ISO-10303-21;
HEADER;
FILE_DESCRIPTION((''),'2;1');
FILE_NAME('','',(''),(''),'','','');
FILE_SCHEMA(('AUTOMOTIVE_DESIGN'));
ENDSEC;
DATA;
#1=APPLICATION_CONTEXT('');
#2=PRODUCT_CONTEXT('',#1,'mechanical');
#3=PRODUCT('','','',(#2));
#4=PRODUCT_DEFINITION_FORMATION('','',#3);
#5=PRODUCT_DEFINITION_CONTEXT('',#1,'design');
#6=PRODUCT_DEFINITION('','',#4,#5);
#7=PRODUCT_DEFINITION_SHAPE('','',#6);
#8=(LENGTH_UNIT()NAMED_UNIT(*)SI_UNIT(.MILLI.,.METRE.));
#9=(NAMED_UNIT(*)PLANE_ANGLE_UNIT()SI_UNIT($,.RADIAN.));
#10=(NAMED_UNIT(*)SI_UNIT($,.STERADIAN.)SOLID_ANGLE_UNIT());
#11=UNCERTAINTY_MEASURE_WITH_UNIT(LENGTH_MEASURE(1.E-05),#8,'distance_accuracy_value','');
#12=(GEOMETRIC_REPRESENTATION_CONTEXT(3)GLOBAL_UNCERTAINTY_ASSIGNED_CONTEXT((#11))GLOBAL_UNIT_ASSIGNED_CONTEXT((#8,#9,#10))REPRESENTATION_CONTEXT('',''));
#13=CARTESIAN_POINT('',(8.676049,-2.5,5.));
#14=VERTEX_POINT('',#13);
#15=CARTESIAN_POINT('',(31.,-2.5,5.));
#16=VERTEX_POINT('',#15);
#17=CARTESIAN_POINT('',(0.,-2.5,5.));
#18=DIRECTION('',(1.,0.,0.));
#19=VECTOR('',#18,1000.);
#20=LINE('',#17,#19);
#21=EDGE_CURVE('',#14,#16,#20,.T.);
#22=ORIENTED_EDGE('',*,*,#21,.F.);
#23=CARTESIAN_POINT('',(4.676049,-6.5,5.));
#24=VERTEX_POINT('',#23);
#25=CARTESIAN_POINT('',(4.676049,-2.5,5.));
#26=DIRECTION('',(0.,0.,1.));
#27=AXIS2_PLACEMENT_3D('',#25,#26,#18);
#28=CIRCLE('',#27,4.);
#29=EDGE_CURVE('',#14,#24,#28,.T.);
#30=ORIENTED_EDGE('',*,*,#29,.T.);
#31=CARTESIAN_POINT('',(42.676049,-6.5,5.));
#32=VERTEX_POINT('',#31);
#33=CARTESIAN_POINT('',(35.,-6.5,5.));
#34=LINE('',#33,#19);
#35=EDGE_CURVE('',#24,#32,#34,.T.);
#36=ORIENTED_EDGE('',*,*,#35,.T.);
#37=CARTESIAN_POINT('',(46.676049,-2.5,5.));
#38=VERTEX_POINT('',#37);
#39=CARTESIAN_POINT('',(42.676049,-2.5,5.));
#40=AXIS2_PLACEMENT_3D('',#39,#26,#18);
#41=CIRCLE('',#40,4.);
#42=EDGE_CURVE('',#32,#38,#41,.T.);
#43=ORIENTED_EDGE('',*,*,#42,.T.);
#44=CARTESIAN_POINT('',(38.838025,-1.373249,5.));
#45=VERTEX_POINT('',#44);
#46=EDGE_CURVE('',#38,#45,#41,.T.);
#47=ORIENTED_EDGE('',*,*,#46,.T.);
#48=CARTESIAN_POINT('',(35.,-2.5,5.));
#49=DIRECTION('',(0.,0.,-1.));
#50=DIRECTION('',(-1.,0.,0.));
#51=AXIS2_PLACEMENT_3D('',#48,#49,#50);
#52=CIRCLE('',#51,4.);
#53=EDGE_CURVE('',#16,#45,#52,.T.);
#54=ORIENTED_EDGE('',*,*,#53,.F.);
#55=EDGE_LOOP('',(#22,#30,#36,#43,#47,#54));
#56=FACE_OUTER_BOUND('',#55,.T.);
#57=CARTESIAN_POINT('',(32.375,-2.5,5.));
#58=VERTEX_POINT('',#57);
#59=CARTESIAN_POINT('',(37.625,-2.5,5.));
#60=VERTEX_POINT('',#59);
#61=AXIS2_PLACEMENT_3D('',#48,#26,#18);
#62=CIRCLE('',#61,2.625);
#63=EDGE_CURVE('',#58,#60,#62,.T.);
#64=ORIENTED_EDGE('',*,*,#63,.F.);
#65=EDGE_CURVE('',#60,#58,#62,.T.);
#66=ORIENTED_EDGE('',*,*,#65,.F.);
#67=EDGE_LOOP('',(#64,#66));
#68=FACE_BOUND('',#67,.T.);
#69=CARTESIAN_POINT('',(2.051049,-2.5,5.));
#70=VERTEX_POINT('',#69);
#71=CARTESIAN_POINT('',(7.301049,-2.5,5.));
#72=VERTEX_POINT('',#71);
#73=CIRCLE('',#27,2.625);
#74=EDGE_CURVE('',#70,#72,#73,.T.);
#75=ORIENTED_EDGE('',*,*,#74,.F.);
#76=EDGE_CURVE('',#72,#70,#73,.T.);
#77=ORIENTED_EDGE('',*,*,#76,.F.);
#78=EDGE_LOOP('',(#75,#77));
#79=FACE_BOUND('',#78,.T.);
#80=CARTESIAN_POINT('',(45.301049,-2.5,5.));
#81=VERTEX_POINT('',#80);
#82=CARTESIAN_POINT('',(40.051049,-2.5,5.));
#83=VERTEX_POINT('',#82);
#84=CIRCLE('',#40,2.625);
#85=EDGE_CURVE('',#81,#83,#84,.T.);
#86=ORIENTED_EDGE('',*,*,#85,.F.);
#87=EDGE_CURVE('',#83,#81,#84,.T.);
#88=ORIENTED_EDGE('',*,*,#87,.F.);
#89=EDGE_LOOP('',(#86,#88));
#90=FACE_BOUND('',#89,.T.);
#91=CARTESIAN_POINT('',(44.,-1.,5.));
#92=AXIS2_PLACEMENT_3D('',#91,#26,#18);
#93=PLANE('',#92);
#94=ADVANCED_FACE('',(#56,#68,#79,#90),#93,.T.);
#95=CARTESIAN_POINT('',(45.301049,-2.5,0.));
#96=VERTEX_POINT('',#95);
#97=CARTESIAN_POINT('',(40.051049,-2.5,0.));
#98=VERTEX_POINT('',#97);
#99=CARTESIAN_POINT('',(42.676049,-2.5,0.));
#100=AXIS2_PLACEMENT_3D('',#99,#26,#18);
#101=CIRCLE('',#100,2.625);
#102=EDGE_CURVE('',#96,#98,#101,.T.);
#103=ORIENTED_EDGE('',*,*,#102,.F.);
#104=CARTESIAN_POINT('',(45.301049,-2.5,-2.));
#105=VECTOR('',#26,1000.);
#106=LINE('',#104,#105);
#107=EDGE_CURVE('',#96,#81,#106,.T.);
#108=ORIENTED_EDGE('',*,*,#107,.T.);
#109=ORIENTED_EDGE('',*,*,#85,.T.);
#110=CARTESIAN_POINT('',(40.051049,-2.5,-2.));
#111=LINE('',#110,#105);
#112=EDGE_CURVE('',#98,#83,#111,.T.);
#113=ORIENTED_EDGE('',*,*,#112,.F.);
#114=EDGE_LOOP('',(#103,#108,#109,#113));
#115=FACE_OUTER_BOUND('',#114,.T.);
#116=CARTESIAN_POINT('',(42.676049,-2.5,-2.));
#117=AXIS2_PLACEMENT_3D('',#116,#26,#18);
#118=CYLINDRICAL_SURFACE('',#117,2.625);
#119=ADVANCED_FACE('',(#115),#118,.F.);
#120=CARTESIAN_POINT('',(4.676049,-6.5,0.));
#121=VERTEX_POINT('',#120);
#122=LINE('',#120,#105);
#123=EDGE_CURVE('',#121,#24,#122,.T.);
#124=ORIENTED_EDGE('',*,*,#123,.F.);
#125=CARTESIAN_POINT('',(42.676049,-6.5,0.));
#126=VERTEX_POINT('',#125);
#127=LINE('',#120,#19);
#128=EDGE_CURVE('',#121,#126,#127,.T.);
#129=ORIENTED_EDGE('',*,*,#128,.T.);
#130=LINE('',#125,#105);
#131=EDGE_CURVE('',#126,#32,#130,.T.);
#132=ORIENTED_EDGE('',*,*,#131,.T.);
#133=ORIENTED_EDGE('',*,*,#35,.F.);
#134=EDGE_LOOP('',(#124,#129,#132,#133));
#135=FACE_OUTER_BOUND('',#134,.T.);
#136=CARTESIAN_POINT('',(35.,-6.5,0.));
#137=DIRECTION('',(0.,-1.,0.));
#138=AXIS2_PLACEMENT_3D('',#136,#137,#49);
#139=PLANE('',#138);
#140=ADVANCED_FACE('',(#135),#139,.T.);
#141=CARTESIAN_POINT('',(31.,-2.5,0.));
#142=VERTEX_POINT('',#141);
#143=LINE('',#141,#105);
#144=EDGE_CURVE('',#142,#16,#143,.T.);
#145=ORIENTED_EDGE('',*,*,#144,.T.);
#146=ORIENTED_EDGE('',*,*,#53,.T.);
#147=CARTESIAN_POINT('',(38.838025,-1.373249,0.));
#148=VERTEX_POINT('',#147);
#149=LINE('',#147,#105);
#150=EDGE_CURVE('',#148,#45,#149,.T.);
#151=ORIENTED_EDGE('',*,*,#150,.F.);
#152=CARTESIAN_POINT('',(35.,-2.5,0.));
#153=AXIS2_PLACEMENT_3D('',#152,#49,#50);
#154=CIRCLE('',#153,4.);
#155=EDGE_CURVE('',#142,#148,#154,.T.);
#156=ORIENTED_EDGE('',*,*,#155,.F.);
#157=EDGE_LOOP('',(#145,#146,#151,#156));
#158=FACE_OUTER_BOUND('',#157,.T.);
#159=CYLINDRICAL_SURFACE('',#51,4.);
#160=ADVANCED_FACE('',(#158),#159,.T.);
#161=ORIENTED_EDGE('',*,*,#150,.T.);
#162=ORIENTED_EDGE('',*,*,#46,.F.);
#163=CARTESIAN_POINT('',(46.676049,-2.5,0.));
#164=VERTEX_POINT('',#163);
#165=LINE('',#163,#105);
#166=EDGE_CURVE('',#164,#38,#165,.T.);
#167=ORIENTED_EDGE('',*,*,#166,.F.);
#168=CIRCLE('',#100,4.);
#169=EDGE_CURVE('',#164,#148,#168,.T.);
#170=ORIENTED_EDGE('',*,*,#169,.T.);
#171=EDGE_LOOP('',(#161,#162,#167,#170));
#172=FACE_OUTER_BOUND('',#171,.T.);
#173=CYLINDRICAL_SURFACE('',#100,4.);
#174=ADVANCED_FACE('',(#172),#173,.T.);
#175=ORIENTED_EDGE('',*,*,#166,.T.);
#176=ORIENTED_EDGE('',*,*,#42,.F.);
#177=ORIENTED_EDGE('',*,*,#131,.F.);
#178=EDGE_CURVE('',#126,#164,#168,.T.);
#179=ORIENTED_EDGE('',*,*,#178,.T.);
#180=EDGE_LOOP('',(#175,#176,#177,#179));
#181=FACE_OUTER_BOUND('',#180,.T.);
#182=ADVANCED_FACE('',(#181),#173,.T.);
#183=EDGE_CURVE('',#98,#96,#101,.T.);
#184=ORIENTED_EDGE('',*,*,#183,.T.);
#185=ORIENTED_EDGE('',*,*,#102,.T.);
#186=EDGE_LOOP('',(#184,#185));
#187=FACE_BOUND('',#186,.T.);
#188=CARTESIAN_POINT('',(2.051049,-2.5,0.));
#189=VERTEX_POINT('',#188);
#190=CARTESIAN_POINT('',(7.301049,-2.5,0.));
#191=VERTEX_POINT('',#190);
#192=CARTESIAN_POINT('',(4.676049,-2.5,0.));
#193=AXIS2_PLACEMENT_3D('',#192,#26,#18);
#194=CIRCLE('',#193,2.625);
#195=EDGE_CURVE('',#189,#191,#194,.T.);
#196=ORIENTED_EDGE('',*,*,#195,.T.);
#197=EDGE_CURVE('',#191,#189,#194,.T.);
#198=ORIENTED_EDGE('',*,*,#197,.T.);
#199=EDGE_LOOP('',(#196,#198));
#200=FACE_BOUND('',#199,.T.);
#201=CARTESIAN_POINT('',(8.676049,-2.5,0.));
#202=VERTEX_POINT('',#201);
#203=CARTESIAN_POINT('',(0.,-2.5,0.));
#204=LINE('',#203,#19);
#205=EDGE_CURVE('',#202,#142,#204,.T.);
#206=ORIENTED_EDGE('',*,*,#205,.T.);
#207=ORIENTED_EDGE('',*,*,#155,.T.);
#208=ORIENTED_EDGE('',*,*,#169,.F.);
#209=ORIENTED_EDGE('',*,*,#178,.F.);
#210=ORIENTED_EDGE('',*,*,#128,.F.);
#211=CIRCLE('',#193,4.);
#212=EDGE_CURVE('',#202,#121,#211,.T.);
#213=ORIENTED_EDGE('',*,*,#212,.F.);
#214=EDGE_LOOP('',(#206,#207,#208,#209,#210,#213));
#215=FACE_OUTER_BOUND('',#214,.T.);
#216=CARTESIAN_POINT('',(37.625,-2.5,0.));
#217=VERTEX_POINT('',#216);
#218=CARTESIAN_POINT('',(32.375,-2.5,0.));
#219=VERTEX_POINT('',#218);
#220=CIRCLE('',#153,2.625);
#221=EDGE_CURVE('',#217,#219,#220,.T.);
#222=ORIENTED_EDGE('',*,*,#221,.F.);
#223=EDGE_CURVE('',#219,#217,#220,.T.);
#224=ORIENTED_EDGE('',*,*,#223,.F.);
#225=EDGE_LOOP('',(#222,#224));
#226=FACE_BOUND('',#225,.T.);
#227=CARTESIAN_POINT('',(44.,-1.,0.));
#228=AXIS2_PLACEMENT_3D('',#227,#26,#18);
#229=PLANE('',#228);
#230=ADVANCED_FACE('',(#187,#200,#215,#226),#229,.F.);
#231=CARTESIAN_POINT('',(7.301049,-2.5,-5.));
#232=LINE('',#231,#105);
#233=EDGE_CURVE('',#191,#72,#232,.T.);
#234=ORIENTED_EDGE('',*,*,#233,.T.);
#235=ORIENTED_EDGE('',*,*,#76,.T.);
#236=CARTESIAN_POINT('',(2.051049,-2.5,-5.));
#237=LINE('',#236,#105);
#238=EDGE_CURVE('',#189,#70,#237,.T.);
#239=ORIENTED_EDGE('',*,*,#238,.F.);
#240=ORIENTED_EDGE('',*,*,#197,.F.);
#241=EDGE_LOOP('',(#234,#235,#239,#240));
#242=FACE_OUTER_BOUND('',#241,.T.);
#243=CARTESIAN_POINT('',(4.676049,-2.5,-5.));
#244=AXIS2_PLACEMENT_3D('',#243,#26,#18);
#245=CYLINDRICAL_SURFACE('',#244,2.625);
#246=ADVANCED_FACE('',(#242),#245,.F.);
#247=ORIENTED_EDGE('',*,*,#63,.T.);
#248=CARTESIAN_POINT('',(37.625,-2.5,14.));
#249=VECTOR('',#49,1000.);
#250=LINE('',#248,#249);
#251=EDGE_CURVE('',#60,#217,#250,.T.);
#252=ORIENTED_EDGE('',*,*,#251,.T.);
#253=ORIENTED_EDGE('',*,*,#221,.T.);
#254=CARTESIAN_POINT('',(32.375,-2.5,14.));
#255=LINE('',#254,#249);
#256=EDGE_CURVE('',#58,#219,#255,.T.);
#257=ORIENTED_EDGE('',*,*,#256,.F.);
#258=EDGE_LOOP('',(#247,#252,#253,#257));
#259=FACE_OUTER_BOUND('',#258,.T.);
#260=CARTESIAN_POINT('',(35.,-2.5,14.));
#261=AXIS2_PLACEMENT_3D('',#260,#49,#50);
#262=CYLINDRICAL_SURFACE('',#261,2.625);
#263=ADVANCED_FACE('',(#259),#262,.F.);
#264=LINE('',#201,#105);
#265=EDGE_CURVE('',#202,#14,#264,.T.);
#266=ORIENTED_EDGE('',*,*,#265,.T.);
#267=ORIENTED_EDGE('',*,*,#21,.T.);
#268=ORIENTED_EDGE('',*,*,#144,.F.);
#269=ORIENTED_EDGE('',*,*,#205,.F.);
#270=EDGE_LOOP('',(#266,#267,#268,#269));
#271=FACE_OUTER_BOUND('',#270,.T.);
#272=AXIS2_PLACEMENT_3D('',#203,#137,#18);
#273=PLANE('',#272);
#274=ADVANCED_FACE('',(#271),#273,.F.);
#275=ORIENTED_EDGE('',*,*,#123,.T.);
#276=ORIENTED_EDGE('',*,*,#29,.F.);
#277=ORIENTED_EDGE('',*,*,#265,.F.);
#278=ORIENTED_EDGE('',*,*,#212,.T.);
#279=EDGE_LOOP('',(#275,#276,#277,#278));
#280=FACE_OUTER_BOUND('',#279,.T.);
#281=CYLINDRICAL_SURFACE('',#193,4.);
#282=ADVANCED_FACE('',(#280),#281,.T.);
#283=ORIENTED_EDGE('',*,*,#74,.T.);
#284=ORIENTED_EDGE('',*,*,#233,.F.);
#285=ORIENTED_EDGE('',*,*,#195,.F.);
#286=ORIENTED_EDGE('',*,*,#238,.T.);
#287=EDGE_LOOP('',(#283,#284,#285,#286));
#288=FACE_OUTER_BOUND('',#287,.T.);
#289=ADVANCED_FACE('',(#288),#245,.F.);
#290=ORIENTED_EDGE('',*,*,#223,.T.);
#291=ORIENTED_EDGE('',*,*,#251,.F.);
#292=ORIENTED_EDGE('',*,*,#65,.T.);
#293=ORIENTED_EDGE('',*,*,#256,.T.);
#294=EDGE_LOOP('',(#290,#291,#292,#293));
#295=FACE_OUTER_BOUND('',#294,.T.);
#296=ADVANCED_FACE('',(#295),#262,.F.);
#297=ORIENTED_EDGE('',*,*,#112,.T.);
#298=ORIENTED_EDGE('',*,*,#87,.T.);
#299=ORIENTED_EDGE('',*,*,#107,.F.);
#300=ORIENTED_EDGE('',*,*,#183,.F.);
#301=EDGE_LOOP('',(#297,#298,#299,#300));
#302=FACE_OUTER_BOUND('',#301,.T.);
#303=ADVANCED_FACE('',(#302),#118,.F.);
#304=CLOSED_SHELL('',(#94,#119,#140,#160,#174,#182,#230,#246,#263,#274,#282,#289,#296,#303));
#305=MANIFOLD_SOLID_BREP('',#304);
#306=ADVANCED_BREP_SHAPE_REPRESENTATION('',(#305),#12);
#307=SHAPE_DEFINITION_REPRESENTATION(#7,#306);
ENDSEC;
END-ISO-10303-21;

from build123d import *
from build123d.topology import SkipClean

# Parameters (mm, degrees)
BOSS_EXTRUDE1_DEPTH          = 5
SKETCH2_R                    = 2.5
BOSS_EXTRUDE2_DEPTH          = 7
SKETCH4_R                    = 2.5
BOSS_EXTRUDE4_DEPTH          = 9
SKETCH10_R                   = 2.5
BOSS_EXTRUDE6_DEPTH          = 5
SKETCH13_W                   = 0.75
SKETCH13_H                   = 0.75
CUT_REVOLVE1_ANGLE           = 45
CUT_REVOLVE1_OTHER_WAY_ANGLE = 45
SKETCH15_W                   = 0.75
SKETCH15_H                   = 0.75
CUT_REVOLVE2_ANGLE           = 45
CUT_REVOLVE2_OTHER_WAY_ANGLE = 45
SKETCH17_R                   = 4
BOSS_EXTRUDE7_DEPTH          = 5
SKETCH18_R                   = 2.930859256
CUT_EXTRUDE1_DEPTH           = 7
SKETCH19_R                   = 2.625
CUT_EXTRUDE2_DEPTH           = 7
SKETCH20_R                   = 4
BOSS_EXTRUDE8_DEPTH          = 5
SKETCH21_R                   = 2.625
CUT_EXTRUDE3_DEPTH           = 50.162013496
SKETCH23_R                   = 4
BOSS_EXTRUDE9_DEPTH          = 5
SKETCH24_R                   = 2.625
CUT_EXTRUDE4_DEPTH           = 15
CUT_EXTRUDE5_DEPTH           = 10
CUT_EXTRUDE6_DEPTH           = 48.390965078
BOSS_EXTRUDE10_DEPTH         = 5


with BuildPart() as part:
    # Sketch1 → Boss-Extrude1 (new body)
    with BuildSketch(Plane.XY):
        with BuildLine():
            Line((1, 0), (44, 0))
            ThreePointArc((44, 0), (44.707106781, -0.292893219), (45, -1))
            Line((45, -1), (45, -4))
            ThreePointArc((45, -4), (44.707106781, -4.707106781), (44, -5))
            Line((44, -5), (1, -5))
            ThreePointArc((1, -5), (0.292893219, -4.707106781), (0, -4))
            Line((0, -4), (0, -1))
            ThreePointArc((0, -1), (0.292893219, -0.292893219), (1, 0))
        make_face()
    extrude(amount=BOSS_EXTRUDE1_DEPTH)

    # Sketch2 → Boss-Extrude2 (add)
    with BuildSketch(Plane(origin=(0, 0, 0), x_dir=(-1, 0, 0), z_dir=(0, 0, -1))):
        with Locations(Location((-42.676049222, -2.5, 0), (0, 0, 158.369487395))):
            Circle(SKETCH2_R)
    extrude(amount=BOSS_EXTRUDE2_DEPTH)

    # Sketch4 → Boss-Extrude4 (add)
    with BuildSketch(Plane.XY.offset(5)):
        with Locations(Location((35, -2.5, 0), (0, 0, 270))):
            Circle(SKETCH4_R)
    extrude(amount=BOSS_EXTRUDE4_DEPTH)

    # Sketch10 → Boss-Extrude6 (add)
    with BuildSketch(Plane.XY.offset(5)):
        with Locations(Location((4.676049222, -2.5, 0), (0, 0, 270))):
            Circle(SKETCH10_R)
    extrude(amount=BOSS_EXTRUDE6_DEPTH)

    # Sketch13 → Cut-Revolve1 (revolve, cut)
    with BuildSketch(Plane(origin=(35, 0, 1.995810748), x_dir=(0, 1, 0), z_dir=(1, 0, 0))):
        with Locations((-0.375, 8.375)):
            Rectangle(SKETCH13_W, SKETCH13_H)
        with Locations((-4.625, 8.375)):
            Rectangle(SKETCH13_W, SKETCH13_H)
    revolve(axis=Axis((35, -2.5, 15.995810748), (0, 0, -1)), revolution_arc=CUT_REVOLVE1_ANGLE, mode=Mode.SUBTRACT)

    # Sketch13 → Cut-Revolve1 other way (revolve, cut)
    with BuildSketch(Plane(origin=(35, 0, 1.995810748), x_dir=(0, 1, 0), z_dir=(1, 0, 0))):
        with Locations((-0.375, 8.375)):
            Rectangle(SKETCH13_W, SKETCH13_H)
        with Locations((-4.625, 8.375)):
            Rectangle(SKETCH13_W, SKETCH13_H)
    revolve(axis=Axis((35, -2.5, 15.995810748), (0, 0, 1)), revolution_arc=CUT_REVOLVE1_OTHER_WAY_ANGLE, mode=Mode.SUBTRACT)

    # Sketch15 → Cut-Revolve2 (revolve, cut)
    with BuildSketch(Plane(origin=(42.676049222, 0, -1.99986967), x_dir=(0, 1, 0), z_dir=(-1, 0, 0))):
        with Locations((-0.375, 3.375)):
            Rectangle(SKETCH15_W, SKETCH15_H)
        with Locations((-4.625, 3.375)):
            Rectangle(SKETCH15_W, SKETCH15_H)
    revolve(axis=Axis((42.676049222, -2.5, -8.99986967), (0, 0, 1)), revolution_arc=CUT_REVOLVE2_ANGLE, mode=Mode.SUBTRACT)

    # Sketch15 → Cut-Revolve2 other way (revolve, cut)
    with BuildSketch(Plane(origin=(42.676049222, 0, -1.99986967), x_dir=(0, 1, 0), z_dir=(-1, 0, 0))):
        with Locations((-0.375, 3.375)):
            Rectangle(SKETCH15_W, SKETCH15_H)
        with Locations((-4.625, 3.375)):
            Rectangle(SKETCH15_W, SKETCH15_H)
    revolve(axis=Axis((42.676049222, -2.5, -8.99986967), (0, 0, -1)), revolution_arc=CUT_REVOLVE2_OTHER_WAY_ANGLE, mode=Mode.SUBTRACT)

    # Sketch17 → Boss-Extrude7 (add)
    with BuildSketch(Plane.XY.offset(5)):
        with Locations((42.676049222, -2.5)):
            Circle(SKETCH17_R)
    extrude(amount=-BOSS_EXTRUDE7_DEPTH)

    # Sketch18 → Cut-Extrude1 (cut)
    with BuildSketch(Plane(origin=(0, 0, -7), x_dir=(-1, 0, 0), z_dir=(0, 0, -1))):
        with Locations((-42.676049222, -2.5)):
            Circle(SKETCH18_R)
    extrude(amount=-CUT_EXTRUDE1_DEPTH, mode=Mode.SUBTRACT)

    # Sketch19 → Cut-Extrude2 (cut)
    with BuildSketch(Plane.XY.offset(5)):
        with Locations((42.676049222, -2.5)):
            Circle(SKETCH19_R)
    extrude(amount=-CUT_EXTRUDE2_DEPTH, mode=Mode.SUBTRACT)

    # Sketch20 → Boss-Extrude8 (add)
    with BuildSketch(Plane(origin=(0, 0, 0), x_dir=(-1, 0, 0), z_dir=(0, 0, -1))):
        with Locations((-35, -2.5)):
            Circle(SKETCH20_R)
    extrude(amount=-BOSS_EXTRUDE8_DEPTH)

    # Sketch21 → Cut-Extrude3 (cut, through all)
    with BuildSketch(Plane(origin=(0, 0, 0), x_dir=(-1, 0, 0), z_dir=(0, 0, -1))):
        with Locations((-35, -2.5)):
            Circle(SKETCH21_R)
    extrude(amount=-CUT_EXTRUDE3_DEPTH, mode=Mode.SUBTRACT)

    # Sketch23 → Boss-Extrude9 (add)
    with BuildSketch(Plane.XY.offset(5)):
        with Locations((4.676049222, -2.5)):
            Circle(SKETCH23_R)
    extrude(amount=-BOSS_EXTRUDE9_DEPTH)

    # Sketch24 → Cut-Extrude4 (cut)
    with BuildSketch(Plane.XY.offset(10)):
        with Locations((4.676049222, -2.5)):
            Circle(SKETCH24_R)
    extrude(amount=-CUT_EXTRUDE4_DEPTH, mode=Mode.SUBTRACT)

    # Sketch25 → Cut-Extrude5 (cut)
    with BuildSketch(Plane.XY.offset(5)):
        with BuildLine():
            Line((1.553550223, -5), (-1.854692679, -7.728778219))
            Line((-1.854692679, -7.728778219), (-3.436521983, -2.874938814))
            Line((-3.436521983, -2.874938814), (-1.53654244, 1.593813071))
            Line((-1.53654244, 1.593813071), (0.676049222, 3.037797523))
            Line((0.676049222, 3.037797523), (1.553550223, 0))
            ThreePointArc((1.553550223, 0), (0.676049222, -2.5), (1.553550223, -5))
        make_face()
    extrude(amount=-CUT_EXTRUDE5_DEPTH, mode=Mode.SUBTRACT)

    # Sketch26 → Cut-Extrude6 (cut, through all)
    with SkipClean():  # the faces are left unmerged after this step: merging them gives an invalid solid
        with BuildSketch(Plane.XY.offset(5)):
            Polygon((31, 2.88382286), (31, 2.910088177), (31.877501001, 0), (7.798548222, 0), align=None)
            with BuildLine():
                Line((39.403739803, 2.542373737), (38.122498999, 0))
                Line((38.122498999, 0), (39.553550223, 0))
                ThreePointArc((39.553550223, 0), (39.704808809, 0.178008664), (39.866200483, 0.346884273))
                Line((39.866200483, 0.346884273), (39.403739803, 2.542373737))
            make_face()
            with BuildLine():
                ThreePointArc((31.877501001, 0), (31.225745372, -1.175235115), (31, -2.5))
                Line((31, -2.5), (8.676049222, -2.5))
                ThreePointArc((8.676049222, -2.5), (8.450303851, -1.175235115), (7.798548222, 0))
                Line((7.798548222, 0), (31.877501001, 0))
            make_face()
            with BuildLine():
                Line((39.553550223, 0), (38.122498999, 0))
                ThreePointArc((38.122498999, 0), (38.547347694, -0.651669851), (38.838024611, -1.373249325))
                ThreePointArc((38.838024611, -1.373249325), (39.128701529, -0.651669851), (39.553550223, 0))
            make_face()
        extrude(amount=-CUT_EXTRUDE6_DEPTH, mode=Mode.SUBTRACT)

    # Sketch27 → Boss-Extrude10 (add, through all)
    with SkipClean():  # the faces are left unmerged after this step: merging them gives an invalid solid
        with BuildSketch(Plane.XY.offset(5)):
            Polygon((4.676049222, -6.5), (35, -6.5), (42.676049222, -6.5), (39.429079082, -3.966331103), (35, -5.966502381), (31.287082695, -3.966331103), (8.288836977, -3.966331103), align=None)
        extrude(amount=-BOSS_EXTRUDE10_DEPTH)


solid = part.part
